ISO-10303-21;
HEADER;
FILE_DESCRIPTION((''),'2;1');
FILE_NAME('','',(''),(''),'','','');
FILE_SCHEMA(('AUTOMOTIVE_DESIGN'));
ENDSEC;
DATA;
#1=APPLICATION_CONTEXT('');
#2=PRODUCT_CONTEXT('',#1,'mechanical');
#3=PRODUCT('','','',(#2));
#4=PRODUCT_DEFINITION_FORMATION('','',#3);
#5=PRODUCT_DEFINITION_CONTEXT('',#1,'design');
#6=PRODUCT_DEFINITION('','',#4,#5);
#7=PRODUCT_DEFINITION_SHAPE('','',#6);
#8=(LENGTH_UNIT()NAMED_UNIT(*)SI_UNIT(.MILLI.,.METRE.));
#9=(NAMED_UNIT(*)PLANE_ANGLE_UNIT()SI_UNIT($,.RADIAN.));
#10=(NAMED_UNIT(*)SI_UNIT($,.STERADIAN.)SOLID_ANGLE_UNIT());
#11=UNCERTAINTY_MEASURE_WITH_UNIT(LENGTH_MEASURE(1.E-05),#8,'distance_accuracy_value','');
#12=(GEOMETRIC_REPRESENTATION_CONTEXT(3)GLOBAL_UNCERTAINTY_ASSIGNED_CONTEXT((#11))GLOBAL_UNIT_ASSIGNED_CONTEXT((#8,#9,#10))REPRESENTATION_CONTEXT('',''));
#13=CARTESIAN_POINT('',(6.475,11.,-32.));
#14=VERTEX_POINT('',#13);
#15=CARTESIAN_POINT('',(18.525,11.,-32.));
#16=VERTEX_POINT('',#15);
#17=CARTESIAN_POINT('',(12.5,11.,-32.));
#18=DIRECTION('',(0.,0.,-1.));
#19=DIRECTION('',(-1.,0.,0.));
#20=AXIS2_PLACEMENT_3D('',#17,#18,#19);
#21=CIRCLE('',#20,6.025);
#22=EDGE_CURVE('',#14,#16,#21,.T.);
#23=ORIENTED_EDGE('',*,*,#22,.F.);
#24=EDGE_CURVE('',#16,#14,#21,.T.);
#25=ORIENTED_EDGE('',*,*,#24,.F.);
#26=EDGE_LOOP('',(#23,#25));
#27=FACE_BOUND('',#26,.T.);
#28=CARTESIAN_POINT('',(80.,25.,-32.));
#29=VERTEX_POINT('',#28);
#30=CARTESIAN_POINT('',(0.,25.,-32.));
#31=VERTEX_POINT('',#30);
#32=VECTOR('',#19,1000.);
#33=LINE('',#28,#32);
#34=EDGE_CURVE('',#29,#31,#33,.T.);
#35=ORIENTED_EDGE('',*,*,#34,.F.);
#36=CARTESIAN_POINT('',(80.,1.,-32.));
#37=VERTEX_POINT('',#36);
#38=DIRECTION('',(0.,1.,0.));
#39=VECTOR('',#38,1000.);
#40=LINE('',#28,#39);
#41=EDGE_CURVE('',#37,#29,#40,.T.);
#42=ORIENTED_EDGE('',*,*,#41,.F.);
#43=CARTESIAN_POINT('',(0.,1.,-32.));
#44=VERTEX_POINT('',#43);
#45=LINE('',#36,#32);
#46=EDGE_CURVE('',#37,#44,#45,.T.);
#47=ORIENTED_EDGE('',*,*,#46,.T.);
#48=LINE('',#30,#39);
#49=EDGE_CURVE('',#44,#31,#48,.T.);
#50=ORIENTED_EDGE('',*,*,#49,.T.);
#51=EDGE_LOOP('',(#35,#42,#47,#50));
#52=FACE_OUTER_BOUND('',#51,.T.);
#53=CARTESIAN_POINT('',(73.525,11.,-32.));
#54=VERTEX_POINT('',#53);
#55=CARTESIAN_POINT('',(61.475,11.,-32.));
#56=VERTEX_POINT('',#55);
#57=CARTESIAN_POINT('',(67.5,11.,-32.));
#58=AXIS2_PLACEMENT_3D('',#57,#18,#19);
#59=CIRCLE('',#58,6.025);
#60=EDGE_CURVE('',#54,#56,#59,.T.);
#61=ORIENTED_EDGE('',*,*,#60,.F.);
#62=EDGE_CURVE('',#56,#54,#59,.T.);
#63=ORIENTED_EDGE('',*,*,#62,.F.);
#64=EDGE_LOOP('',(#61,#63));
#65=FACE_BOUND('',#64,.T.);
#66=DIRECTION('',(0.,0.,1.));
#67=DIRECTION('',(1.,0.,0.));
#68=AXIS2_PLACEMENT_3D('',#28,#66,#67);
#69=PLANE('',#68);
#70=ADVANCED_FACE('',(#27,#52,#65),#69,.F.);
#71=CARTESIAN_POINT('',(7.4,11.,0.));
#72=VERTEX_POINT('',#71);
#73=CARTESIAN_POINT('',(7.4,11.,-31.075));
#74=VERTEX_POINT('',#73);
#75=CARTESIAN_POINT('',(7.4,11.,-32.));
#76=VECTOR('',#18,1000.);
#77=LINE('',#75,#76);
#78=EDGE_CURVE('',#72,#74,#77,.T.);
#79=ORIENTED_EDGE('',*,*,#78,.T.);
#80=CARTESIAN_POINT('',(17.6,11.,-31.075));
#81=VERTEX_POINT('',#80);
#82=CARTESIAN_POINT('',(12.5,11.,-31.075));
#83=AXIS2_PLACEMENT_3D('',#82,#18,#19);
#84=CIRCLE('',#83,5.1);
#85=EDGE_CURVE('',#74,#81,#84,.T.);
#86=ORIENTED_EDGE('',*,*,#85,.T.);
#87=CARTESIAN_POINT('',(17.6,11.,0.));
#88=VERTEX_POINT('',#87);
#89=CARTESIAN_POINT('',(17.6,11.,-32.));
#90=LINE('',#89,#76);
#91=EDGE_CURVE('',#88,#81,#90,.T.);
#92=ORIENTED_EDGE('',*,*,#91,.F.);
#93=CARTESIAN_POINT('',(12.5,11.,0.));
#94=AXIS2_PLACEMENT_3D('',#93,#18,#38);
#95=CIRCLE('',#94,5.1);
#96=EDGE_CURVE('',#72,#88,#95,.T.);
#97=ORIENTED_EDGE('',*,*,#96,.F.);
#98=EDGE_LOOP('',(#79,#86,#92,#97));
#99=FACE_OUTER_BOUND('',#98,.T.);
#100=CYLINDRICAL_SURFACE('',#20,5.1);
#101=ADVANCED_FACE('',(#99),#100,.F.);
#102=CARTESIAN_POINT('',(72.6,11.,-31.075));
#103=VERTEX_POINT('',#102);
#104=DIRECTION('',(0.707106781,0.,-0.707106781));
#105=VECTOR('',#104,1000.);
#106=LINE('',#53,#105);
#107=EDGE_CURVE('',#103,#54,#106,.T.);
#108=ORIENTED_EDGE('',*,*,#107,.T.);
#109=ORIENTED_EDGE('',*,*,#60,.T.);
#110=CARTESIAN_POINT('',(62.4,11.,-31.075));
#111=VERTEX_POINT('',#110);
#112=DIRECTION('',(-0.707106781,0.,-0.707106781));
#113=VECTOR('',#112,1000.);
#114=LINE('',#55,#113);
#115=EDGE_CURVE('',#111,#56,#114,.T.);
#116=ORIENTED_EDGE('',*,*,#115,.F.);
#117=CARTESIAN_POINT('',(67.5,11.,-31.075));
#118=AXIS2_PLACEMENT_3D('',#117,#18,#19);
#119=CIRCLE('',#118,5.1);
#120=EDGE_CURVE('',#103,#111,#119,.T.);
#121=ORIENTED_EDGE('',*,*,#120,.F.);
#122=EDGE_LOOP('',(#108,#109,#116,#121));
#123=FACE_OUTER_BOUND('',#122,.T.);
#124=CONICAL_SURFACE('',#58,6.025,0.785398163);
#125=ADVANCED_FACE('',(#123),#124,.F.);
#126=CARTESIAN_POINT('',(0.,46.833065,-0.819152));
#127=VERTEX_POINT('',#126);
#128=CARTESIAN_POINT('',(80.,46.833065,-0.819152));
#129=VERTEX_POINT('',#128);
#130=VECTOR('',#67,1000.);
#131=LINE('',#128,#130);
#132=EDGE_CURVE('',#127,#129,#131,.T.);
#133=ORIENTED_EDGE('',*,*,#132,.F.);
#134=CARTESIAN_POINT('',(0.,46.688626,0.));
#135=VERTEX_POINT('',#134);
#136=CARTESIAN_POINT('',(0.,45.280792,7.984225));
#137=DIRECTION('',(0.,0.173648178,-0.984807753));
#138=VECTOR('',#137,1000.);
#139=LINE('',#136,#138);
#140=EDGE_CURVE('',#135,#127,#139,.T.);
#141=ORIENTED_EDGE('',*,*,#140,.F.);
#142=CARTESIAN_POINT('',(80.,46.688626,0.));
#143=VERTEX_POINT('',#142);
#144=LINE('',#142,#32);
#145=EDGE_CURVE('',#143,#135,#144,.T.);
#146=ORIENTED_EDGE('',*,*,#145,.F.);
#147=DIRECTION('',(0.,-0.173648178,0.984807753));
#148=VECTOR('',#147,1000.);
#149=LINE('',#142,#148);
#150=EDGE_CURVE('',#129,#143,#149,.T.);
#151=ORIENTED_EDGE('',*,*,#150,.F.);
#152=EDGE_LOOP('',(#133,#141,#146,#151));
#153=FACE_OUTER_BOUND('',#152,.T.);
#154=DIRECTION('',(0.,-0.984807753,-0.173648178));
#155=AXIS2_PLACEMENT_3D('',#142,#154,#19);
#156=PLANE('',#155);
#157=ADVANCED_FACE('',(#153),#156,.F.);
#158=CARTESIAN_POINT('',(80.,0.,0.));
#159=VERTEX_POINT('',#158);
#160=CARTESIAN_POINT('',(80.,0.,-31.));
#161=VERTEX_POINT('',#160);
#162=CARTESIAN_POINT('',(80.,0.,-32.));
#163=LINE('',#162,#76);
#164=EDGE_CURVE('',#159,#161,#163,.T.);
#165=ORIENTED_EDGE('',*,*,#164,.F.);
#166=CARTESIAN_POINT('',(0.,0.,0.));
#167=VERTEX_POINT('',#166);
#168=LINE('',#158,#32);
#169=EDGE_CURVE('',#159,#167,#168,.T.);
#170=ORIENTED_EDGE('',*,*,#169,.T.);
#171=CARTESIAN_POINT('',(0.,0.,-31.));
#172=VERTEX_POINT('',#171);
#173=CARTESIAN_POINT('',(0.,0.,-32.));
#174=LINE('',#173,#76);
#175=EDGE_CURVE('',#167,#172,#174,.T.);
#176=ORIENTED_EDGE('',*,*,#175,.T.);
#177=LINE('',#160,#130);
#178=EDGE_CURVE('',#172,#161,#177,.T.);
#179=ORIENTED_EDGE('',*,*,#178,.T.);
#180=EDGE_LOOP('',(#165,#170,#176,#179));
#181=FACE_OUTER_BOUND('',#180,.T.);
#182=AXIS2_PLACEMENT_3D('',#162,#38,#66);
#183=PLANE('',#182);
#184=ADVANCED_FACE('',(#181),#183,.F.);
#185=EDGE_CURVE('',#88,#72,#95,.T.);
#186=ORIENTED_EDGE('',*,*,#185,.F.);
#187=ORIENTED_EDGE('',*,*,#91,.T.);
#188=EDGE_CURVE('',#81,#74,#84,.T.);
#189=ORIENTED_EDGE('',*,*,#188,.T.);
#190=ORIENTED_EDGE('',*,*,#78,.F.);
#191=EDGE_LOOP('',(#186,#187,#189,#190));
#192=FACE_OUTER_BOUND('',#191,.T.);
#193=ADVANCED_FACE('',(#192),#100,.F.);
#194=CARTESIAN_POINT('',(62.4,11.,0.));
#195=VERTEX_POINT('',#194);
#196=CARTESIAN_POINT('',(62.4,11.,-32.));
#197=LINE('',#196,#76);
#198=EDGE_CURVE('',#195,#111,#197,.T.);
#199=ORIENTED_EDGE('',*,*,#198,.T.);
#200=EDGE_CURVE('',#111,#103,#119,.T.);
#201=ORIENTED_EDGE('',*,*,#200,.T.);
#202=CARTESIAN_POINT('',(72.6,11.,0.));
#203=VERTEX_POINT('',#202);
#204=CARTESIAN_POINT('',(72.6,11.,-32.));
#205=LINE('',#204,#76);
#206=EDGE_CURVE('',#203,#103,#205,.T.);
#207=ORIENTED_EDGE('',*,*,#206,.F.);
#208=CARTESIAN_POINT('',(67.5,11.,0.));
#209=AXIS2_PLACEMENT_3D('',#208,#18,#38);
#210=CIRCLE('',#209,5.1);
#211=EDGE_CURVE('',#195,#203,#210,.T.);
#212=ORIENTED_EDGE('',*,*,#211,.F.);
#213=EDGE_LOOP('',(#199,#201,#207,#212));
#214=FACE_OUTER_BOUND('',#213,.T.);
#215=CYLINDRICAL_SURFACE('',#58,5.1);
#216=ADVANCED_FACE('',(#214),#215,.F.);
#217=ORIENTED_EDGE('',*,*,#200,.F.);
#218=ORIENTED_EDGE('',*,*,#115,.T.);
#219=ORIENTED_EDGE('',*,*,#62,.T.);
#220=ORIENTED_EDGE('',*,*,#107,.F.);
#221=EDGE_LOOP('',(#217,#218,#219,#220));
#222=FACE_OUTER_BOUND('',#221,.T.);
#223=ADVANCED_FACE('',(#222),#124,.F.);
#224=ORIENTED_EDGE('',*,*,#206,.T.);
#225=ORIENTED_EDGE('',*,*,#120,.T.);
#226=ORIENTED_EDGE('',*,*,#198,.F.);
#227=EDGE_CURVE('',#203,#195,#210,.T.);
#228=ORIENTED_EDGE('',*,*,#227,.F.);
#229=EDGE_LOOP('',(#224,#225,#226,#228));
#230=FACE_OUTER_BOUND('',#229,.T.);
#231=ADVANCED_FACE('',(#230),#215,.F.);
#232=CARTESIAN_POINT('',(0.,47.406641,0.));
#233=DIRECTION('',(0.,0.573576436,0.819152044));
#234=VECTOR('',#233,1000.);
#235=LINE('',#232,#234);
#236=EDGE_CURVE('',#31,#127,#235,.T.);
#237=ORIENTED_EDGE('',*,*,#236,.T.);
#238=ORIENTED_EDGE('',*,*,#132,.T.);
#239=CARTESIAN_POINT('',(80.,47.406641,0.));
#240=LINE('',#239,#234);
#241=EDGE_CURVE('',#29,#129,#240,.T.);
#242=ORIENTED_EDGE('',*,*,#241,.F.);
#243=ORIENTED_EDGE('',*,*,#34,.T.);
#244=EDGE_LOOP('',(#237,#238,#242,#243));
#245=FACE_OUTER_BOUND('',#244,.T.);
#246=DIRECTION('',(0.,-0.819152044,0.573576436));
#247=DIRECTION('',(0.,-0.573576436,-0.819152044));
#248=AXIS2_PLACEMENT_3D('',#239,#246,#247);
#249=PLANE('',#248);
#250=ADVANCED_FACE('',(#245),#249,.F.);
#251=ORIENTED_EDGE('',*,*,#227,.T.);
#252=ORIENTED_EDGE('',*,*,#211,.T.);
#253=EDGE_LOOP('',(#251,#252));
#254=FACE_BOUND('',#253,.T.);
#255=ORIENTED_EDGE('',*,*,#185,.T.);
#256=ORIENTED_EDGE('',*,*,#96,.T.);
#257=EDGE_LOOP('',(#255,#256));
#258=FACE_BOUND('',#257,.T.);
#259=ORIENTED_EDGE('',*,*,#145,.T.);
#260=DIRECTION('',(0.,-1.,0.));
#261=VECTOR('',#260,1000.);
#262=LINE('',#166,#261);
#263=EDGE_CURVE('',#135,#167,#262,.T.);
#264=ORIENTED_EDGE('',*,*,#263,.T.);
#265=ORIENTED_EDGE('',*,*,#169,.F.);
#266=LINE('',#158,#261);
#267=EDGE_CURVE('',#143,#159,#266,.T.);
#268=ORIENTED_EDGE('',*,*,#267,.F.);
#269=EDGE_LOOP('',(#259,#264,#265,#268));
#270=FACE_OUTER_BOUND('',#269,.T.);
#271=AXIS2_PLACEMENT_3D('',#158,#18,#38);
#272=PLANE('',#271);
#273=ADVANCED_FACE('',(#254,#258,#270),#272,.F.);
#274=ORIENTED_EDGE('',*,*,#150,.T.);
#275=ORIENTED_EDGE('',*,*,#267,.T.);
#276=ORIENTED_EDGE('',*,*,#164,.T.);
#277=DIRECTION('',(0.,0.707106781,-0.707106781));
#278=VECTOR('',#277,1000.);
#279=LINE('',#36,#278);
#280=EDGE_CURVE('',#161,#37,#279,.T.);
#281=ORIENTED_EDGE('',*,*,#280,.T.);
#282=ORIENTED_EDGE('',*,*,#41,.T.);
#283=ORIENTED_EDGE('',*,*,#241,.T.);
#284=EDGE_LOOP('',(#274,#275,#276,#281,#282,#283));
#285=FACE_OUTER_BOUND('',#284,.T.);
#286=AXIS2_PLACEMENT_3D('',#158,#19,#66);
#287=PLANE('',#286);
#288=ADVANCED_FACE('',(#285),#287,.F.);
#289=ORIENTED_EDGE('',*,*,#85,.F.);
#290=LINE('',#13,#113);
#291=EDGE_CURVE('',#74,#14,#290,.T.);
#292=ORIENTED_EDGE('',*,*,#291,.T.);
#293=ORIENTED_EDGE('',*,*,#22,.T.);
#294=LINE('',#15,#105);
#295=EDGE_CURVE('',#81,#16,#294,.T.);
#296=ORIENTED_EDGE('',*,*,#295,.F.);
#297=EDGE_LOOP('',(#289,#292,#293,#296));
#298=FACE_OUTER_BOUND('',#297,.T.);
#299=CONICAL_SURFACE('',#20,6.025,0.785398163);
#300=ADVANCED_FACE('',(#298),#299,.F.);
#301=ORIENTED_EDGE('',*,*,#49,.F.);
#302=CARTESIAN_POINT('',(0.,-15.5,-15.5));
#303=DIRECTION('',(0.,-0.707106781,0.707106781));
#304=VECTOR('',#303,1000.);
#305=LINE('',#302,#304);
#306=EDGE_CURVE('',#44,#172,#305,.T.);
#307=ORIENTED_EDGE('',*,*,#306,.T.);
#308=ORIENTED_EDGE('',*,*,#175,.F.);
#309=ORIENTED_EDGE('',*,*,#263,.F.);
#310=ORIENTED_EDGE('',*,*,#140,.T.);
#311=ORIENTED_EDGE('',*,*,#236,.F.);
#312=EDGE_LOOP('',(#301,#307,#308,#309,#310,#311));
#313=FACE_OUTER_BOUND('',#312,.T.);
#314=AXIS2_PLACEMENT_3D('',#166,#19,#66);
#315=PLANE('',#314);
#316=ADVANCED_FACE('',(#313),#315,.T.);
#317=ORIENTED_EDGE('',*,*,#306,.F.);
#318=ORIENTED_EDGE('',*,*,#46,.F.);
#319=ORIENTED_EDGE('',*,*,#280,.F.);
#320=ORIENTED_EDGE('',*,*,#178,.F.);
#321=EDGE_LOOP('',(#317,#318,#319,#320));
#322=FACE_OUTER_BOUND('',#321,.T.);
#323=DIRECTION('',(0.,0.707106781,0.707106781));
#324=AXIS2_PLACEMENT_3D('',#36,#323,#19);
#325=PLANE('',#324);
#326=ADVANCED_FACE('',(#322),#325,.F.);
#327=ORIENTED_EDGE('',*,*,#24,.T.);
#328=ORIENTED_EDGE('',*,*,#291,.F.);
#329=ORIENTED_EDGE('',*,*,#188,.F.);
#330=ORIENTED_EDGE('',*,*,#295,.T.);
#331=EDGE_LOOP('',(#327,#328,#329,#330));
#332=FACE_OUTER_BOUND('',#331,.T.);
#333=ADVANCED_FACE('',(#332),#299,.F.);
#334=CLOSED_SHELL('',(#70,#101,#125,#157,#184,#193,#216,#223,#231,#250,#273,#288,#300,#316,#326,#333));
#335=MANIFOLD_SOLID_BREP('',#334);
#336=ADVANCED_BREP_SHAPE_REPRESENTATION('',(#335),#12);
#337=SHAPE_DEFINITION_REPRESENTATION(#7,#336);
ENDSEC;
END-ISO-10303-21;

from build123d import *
from OCP.BRepFilletAPI import BRepFilletAPI_MakeChamfer

# Parameters (mm, degrees)
BOSS_EXTRUDE1_DEPTH = 80
CHAMFER1_SIZE       = 1
CHAMFER1_SIZE2      = 0.718015043


with BuildPart() as part:
    # Sketch1 → Boss-Extrude1 (new body)
    with BuildSketch(Plane(origin=(0, 0, 0), x_dir=(0, 0, -1), z_dir=(1, 0, 0))):
        Polygon((0, 0), (0, 47.406641223), (32, 25), (32, 0), align=None)
    extrude(amount=BOSS_EXTRUDE1_DEPTH)

    # Sketch3 → M12 Tapped Hole1 (revolve, cut)
    with BuildSketch(Plane(origin=(12.5, 11, -32), x_dir=(0, 1, 0), z_dir=(1, 0, 0))):
        Polygon((0, 0), (0, 63.064389157), (5.1, 60), (5.1, 0.925), (6.025, 0), align=None)
    m12_tapped_hole1 = revolve(axis=Axis((12.5, 11, -38.35), (0, 0, 1)), mode=Mode.SUBTRACT)

    # Mirror1: M12 Tapped Hole1 across plane
    add(m12_tapped_hole1.mirror(Plane(origin=(40, 0, 0), x_dir=(0, 0, 1), z_dir=(1, 0, 0))), mode=Mode.SUBTRACT)

    # Chamfer1: one chamfer whose edges measure the first distance from different faces: ONE call of the kernel's chamfer builder (chamfer() names one face for all edges)
    chamfer1_edges_1 = [part.edges().sort_by_distance(p)[0] for p in [
        (40, 47.406641223, 0),
    ]]
    chamfer1_side_1 = [part.faces().sort_by_distance(p)[0] for p in [
        (40, 36.203320611, -16),
    ]]
    chamfer1_edges_2 = [part.edges().sort_by_distance(p)[0] for p in [
        (40, 0, -32),
    ]]
    chamfer1 = BRepFilletAPI_MakeChamfer(part.part.solid().wrapped)
    for e in chamfer1_edges_1:
        chamfer1.Add(CHAMFER1_SIZE, CHAMFER1_SIZE2, e.wrapped, chamfer1_side_1[0].wrapped)  # the first distance lies on this face
    for e in chamfer1_edges_2:
        chamfer1.Add(CHAMFER1_SIZE, e.wrapped)
    add(Compound.cast(chamfer1.Shape()), mode=Mode.REPLACE)


solid = part.part
